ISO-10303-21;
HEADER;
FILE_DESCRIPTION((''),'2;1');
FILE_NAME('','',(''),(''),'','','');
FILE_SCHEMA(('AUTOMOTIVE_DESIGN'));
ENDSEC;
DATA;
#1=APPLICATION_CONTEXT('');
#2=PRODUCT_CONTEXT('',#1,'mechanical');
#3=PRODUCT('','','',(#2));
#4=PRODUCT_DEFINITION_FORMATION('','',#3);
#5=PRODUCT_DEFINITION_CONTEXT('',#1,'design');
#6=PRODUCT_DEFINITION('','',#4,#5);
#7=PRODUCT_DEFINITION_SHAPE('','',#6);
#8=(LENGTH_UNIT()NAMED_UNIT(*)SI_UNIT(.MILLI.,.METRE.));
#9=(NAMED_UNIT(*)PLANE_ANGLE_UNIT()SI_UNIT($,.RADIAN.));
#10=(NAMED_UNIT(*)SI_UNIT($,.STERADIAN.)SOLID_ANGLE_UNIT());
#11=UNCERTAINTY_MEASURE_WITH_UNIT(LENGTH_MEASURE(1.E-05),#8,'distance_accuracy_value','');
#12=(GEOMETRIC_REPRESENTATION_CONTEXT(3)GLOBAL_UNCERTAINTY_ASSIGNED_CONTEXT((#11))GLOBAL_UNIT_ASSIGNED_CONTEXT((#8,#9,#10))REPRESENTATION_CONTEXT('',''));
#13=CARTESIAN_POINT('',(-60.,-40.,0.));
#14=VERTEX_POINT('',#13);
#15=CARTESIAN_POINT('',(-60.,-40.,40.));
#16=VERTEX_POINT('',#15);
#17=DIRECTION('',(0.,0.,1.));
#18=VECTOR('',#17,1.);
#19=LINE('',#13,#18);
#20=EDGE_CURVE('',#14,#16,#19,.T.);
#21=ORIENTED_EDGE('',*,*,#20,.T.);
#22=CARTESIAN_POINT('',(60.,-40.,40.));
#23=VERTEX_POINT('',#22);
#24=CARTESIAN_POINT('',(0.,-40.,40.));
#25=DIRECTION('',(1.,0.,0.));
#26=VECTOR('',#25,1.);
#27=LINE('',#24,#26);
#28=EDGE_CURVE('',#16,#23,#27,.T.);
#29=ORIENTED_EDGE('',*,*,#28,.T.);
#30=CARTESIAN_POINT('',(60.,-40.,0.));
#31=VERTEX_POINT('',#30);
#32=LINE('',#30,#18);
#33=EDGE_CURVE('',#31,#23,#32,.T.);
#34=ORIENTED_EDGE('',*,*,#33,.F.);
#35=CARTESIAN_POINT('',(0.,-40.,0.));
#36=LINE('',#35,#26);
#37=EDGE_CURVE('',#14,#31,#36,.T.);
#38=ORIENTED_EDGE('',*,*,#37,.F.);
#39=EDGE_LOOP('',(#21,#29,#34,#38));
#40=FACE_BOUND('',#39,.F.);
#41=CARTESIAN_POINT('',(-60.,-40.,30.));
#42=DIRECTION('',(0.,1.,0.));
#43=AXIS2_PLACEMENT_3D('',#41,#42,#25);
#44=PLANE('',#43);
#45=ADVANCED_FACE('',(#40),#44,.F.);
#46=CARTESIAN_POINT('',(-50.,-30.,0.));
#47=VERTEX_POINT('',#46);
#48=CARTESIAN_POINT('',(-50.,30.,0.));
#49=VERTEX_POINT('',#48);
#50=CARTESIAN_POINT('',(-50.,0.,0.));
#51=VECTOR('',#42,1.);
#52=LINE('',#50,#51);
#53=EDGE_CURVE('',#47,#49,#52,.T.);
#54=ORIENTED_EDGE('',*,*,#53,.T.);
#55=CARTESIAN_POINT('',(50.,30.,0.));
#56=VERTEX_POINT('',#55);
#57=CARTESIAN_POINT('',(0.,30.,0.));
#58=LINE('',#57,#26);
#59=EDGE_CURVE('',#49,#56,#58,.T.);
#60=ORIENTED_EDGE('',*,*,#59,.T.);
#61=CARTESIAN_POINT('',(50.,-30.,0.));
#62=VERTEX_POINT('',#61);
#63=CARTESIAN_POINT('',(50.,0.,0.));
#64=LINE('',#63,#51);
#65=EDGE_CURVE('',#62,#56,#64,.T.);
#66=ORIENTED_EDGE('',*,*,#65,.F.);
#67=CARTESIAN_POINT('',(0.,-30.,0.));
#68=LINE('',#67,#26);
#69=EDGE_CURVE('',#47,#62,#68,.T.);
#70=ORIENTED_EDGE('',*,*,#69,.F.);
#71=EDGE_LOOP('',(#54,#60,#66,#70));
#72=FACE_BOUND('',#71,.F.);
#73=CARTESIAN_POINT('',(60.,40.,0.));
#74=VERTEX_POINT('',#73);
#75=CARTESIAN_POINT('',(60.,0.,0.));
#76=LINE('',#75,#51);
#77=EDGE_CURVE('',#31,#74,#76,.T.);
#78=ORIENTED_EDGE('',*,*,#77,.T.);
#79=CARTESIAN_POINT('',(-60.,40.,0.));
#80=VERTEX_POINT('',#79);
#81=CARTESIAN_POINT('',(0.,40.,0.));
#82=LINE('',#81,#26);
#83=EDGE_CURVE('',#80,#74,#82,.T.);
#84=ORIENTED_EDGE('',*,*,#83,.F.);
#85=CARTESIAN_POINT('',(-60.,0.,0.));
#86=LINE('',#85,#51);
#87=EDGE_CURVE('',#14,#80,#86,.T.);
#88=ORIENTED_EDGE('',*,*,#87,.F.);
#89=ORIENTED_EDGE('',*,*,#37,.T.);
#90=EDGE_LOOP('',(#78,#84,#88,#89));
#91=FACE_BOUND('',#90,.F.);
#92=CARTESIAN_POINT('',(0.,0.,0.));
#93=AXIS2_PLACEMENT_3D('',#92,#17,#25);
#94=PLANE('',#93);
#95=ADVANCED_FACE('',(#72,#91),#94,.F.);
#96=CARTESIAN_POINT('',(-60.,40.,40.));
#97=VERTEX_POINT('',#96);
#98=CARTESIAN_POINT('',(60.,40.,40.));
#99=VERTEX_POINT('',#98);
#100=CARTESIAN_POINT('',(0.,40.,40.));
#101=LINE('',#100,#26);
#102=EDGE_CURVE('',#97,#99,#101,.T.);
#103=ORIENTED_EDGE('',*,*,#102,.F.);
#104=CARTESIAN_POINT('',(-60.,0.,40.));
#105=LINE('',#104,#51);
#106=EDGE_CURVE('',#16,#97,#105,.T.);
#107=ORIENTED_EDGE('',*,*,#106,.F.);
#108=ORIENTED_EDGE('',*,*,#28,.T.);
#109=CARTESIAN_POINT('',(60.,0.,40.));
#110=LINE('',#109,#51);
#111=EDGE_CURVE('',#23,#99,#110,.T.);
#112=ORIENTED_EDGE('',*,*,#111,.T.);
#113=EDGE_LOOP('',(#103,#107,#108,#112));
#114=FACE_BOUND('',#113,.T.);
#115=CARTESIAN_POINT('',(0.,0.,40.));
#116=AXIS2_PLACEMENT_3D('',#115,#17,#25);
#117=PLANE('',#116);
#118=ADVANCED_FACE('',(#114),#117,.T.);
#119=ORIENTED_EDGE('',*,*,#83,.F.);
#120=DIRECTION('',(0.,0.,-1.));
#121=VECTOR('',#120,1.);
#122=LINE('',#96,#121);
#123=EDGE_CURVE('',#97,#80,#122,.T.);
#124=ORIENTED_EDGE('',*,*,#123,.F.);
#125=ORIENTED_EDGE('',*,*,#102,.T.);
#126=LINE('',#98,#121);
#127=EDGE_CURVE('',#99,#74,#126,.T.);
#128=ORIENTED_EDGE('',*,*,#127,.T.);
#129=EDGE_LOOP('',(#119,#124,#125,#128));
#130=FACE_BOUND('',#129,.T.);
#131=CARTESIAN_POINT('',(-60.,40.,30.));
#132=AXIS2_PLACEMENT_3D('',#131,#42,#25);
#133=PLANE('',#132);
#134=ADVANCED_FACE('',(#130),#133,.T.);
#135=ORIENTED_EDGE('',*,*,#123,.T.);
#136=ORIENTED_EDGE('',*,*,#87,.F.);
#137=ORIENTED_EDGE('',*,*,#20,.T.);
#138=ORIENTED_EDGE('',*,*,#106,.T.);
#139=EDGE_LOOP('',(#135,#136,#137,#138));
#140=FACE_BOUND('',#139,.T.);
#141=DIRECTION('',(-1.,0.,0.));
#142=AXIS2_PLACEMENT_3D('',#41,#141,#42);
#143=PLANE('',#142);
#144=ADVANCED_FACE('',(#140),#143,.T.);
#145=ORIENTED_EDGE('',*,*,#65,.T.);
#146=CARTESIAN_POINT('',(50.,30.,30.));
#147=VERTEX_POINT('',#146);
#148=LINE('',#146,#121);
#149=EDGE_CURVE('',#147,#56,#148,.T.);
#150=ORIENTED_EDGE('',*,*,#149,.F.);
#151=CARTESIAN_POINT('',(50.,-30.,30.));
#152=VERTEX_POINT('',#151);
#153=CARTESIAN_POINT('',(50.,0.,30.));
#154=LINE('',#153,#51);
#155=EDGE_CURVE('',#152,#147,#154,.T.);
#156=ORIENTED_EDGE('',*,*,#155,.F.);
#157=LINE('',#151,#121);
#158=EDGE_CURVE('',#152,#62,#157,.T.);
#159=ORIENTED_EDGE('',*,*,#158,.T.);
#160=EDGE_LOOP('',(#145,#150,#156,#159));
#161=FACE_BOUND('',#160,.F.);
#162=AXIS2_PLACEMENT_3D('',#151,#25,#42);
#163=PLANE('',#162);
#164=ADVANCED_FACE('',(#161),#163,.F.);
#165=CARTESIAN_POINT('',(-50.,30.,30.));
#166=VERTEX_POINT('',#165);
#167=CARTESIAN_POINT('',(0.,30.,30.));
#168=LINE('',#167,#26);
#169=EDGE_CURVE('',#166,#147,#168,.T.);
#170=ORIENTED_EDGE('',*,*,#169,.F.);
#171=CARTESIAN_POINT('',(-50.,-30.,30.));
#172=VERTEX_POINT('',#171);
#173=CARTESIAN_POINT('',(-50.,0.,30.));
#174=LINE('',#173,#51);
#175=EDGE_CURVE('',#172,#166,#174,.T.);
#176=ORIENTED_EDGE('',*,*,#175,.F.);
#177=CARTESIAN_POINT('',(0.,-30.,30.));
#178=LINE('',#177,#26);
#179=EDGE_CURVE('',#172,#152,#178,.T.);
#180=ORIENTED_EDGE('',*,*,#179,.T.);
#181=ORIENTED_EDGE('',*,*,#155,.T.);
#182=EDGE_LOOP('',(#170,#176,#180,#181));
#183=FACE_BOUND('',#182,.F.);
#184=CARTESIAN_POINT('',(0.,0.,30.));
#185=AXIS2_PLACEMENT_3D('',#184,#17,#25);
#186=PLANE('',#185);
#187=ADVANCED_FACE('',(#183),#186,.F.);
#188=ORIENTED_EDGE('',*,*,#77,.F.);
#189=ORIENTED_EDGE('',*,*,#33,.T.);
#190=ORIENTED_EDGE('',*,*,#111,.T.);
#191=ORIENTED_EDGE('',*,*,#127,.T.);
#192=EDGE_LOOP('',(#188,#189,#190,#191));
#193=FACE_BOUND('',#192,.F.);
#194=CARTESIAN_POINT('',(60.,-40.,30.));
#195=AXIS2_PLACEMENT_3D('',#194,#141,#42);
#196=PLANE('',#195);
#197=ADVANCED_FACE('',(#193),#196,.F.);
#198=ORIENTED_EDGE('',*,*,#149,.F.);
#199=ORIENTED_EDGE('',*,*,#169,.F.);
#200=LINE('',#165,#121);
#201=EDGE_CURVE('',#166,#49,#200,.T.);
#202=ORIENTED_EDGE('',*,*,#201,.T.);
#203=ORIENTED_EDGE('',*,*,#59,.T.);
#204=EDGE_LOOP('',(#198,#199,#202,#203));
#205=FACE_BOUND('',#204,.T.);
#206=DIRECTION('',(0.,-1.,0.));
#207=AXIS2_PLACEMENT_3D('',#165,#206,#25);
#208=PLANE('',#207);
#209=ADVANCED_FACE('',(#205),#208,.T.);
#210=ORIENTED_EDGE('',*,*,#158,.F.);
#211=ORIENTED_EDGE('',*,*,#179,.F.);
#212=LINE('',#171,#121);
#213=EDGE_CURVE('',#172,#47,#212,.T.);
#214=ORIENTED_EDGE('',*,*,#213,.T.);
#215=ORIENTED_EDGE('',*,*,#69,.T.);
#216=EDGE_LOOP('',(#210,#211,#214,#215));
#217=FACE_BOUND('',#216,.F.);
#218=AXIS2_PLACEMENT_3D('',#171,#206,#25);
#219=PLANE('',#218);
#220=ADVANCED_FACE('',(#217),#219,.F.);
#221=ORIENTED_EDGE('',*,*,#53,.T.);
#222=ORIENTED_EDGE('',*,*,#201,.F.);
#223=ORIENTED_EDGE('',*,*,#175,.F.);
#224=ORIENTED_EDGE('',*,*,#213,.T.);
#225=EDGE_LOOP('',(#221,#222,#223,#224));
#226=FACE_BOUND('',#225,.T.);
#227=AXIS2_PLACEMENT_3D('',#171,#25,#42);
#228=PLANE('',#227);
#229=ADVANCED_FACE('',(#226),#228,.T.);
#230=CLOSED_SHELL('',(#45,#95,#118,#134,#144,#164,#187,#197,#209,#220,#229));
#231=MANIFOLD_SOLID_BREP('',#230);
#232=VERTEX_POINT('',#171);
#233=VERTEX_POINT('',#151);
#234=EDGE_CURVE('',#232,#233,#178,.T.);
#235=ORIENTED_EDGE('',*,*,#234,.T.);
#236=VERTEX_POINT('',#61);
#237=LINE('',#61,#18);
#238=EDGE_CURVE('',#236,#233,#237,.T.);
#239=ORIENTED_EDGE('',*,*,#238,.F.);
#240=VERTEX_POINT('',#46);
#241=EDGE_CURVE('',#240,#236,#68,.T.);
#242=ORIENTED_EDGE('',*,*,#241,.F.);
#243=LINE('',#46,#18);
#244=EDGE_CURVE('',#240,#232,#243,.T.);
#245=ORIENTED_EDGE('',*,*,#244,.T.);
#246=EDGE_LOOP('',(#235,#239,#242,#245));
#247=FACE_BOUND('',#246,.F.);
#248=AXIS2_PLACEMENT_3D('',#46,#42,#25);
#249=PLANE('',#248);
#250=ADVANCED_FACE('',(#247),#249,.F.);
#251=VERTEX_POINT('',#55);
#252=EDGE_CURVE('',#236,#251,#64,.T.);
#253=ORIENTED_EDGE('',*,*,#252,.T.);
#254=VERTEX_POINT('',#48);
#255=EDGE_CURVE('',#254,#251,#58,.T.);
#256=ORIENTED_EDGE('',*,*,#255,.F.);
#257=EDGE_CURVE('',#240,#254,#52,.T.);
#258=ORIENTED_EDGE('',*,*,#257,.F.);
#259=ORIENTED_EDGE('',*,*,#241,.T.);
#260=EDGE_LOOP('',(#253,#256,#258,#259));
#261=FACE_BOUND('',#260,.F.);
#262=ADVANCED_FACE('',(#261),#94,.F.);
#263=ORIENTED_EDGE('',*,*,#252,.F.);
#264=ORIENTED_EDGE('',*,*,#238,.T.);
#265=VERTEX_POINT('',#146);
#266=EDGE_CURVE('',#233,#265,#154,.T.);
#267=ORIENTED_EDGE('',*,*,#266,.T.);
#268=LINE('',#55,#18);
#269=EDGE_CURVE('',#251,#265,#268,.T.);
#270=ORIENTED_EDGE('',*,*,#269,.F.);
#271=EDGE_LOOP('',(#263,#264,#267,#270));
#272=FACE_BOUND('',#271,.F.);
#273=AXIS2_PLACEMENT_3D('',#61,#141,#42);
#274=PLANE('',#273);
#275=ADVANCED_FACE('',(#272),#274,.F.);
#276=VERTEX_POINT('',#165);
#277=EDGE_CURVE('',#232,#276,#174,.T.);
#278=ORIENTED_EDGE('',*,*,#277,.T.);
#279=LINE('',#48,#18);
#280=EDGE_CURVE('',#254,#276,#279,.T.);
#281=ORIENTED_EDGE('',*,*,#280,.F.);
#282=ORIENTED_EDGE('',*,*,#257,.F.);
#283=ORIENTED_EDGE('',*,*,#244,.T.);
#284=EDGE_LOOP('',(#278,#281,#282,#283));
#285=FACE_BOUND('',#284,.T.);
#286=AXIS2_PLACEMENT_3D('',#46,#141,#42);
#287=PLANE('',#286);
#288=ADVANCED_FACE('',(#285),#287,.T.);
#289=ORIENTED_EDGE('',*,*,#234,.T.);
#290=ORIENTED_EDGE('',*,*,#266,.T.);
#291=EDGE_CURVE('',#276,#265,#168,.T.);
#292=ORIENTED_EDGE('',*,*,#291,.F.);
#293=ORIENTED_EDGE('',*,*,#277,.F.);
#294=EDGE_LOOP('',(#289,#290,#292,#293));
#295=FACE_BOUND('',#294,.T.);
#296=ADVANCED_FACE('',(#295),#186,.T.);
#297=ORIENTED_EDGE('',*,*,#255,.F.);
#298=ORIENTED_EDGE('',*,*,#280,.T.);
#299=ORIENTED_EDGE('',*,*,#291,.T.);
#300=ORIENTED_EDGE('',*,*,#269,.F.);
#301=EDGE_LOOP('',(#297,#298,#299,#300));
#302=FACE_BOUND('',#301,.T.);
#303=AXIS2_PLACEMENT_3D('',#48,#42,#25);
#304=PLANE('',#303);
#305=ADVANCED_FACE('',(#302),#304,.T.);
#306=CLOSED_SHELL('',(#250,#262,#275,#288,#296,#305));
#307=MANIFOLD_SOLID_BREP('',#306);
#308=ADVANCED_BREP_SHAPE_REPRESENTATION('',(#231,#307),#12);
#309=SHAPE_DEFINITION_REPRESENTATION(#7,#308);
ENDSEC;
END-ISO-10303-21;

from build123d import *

# Parameters (mm, degrees)
SKETCH1_W           = 100
SKETCH1_H           = 60
BOSS_EXTRUDE1_DEPTH = 30
SKETCH2_W           = 120
SKETCH2_H           = 80
SKETCH2_W_2         = 100
SKETCH2_H_2         = 60
BOSS_EXTRUDE2_DEPTH = 30
SKETCH3_W           = 120
SKETCH3_H           = 80
BOSS_EXTRUDE3_DEPTH = 10


with BuildPart() as part:
    # Sketch1 → Boss-Extrude1 (new body)
    with BuildSketch(Plane.XY):
        Rectangle(SKETCH1_W, SKETCH1_H)
    extrude(amount=BOSS_EXTRUDE1_DEPTH)


with BuildPart() as body_2:
    # Sketch2 → Boss-Extrude2 (new body)
    with BuildSketch(Plane.XY.offset(30)):
        Rectangle(SKETCH2_W, SKETCH2_H)
        Rectangle(SKETCH2_W_2, SKETCH2_H_2, mode=Mode.SUBTRACT)
    extrude(amount=-BOSS_EXTRUDE2_DEPTH)

    # Sketch3 → Boss-Extrude3 (add)
    with BuildSketch(Plane.XY.offset(30)):
        Rectangle(SKETCH3_W, SKETCH3_H)
    extrude(amount=BOSS_EXTRUDE3_DEPTH)


solid = Compound([part.part, body_2.part])
